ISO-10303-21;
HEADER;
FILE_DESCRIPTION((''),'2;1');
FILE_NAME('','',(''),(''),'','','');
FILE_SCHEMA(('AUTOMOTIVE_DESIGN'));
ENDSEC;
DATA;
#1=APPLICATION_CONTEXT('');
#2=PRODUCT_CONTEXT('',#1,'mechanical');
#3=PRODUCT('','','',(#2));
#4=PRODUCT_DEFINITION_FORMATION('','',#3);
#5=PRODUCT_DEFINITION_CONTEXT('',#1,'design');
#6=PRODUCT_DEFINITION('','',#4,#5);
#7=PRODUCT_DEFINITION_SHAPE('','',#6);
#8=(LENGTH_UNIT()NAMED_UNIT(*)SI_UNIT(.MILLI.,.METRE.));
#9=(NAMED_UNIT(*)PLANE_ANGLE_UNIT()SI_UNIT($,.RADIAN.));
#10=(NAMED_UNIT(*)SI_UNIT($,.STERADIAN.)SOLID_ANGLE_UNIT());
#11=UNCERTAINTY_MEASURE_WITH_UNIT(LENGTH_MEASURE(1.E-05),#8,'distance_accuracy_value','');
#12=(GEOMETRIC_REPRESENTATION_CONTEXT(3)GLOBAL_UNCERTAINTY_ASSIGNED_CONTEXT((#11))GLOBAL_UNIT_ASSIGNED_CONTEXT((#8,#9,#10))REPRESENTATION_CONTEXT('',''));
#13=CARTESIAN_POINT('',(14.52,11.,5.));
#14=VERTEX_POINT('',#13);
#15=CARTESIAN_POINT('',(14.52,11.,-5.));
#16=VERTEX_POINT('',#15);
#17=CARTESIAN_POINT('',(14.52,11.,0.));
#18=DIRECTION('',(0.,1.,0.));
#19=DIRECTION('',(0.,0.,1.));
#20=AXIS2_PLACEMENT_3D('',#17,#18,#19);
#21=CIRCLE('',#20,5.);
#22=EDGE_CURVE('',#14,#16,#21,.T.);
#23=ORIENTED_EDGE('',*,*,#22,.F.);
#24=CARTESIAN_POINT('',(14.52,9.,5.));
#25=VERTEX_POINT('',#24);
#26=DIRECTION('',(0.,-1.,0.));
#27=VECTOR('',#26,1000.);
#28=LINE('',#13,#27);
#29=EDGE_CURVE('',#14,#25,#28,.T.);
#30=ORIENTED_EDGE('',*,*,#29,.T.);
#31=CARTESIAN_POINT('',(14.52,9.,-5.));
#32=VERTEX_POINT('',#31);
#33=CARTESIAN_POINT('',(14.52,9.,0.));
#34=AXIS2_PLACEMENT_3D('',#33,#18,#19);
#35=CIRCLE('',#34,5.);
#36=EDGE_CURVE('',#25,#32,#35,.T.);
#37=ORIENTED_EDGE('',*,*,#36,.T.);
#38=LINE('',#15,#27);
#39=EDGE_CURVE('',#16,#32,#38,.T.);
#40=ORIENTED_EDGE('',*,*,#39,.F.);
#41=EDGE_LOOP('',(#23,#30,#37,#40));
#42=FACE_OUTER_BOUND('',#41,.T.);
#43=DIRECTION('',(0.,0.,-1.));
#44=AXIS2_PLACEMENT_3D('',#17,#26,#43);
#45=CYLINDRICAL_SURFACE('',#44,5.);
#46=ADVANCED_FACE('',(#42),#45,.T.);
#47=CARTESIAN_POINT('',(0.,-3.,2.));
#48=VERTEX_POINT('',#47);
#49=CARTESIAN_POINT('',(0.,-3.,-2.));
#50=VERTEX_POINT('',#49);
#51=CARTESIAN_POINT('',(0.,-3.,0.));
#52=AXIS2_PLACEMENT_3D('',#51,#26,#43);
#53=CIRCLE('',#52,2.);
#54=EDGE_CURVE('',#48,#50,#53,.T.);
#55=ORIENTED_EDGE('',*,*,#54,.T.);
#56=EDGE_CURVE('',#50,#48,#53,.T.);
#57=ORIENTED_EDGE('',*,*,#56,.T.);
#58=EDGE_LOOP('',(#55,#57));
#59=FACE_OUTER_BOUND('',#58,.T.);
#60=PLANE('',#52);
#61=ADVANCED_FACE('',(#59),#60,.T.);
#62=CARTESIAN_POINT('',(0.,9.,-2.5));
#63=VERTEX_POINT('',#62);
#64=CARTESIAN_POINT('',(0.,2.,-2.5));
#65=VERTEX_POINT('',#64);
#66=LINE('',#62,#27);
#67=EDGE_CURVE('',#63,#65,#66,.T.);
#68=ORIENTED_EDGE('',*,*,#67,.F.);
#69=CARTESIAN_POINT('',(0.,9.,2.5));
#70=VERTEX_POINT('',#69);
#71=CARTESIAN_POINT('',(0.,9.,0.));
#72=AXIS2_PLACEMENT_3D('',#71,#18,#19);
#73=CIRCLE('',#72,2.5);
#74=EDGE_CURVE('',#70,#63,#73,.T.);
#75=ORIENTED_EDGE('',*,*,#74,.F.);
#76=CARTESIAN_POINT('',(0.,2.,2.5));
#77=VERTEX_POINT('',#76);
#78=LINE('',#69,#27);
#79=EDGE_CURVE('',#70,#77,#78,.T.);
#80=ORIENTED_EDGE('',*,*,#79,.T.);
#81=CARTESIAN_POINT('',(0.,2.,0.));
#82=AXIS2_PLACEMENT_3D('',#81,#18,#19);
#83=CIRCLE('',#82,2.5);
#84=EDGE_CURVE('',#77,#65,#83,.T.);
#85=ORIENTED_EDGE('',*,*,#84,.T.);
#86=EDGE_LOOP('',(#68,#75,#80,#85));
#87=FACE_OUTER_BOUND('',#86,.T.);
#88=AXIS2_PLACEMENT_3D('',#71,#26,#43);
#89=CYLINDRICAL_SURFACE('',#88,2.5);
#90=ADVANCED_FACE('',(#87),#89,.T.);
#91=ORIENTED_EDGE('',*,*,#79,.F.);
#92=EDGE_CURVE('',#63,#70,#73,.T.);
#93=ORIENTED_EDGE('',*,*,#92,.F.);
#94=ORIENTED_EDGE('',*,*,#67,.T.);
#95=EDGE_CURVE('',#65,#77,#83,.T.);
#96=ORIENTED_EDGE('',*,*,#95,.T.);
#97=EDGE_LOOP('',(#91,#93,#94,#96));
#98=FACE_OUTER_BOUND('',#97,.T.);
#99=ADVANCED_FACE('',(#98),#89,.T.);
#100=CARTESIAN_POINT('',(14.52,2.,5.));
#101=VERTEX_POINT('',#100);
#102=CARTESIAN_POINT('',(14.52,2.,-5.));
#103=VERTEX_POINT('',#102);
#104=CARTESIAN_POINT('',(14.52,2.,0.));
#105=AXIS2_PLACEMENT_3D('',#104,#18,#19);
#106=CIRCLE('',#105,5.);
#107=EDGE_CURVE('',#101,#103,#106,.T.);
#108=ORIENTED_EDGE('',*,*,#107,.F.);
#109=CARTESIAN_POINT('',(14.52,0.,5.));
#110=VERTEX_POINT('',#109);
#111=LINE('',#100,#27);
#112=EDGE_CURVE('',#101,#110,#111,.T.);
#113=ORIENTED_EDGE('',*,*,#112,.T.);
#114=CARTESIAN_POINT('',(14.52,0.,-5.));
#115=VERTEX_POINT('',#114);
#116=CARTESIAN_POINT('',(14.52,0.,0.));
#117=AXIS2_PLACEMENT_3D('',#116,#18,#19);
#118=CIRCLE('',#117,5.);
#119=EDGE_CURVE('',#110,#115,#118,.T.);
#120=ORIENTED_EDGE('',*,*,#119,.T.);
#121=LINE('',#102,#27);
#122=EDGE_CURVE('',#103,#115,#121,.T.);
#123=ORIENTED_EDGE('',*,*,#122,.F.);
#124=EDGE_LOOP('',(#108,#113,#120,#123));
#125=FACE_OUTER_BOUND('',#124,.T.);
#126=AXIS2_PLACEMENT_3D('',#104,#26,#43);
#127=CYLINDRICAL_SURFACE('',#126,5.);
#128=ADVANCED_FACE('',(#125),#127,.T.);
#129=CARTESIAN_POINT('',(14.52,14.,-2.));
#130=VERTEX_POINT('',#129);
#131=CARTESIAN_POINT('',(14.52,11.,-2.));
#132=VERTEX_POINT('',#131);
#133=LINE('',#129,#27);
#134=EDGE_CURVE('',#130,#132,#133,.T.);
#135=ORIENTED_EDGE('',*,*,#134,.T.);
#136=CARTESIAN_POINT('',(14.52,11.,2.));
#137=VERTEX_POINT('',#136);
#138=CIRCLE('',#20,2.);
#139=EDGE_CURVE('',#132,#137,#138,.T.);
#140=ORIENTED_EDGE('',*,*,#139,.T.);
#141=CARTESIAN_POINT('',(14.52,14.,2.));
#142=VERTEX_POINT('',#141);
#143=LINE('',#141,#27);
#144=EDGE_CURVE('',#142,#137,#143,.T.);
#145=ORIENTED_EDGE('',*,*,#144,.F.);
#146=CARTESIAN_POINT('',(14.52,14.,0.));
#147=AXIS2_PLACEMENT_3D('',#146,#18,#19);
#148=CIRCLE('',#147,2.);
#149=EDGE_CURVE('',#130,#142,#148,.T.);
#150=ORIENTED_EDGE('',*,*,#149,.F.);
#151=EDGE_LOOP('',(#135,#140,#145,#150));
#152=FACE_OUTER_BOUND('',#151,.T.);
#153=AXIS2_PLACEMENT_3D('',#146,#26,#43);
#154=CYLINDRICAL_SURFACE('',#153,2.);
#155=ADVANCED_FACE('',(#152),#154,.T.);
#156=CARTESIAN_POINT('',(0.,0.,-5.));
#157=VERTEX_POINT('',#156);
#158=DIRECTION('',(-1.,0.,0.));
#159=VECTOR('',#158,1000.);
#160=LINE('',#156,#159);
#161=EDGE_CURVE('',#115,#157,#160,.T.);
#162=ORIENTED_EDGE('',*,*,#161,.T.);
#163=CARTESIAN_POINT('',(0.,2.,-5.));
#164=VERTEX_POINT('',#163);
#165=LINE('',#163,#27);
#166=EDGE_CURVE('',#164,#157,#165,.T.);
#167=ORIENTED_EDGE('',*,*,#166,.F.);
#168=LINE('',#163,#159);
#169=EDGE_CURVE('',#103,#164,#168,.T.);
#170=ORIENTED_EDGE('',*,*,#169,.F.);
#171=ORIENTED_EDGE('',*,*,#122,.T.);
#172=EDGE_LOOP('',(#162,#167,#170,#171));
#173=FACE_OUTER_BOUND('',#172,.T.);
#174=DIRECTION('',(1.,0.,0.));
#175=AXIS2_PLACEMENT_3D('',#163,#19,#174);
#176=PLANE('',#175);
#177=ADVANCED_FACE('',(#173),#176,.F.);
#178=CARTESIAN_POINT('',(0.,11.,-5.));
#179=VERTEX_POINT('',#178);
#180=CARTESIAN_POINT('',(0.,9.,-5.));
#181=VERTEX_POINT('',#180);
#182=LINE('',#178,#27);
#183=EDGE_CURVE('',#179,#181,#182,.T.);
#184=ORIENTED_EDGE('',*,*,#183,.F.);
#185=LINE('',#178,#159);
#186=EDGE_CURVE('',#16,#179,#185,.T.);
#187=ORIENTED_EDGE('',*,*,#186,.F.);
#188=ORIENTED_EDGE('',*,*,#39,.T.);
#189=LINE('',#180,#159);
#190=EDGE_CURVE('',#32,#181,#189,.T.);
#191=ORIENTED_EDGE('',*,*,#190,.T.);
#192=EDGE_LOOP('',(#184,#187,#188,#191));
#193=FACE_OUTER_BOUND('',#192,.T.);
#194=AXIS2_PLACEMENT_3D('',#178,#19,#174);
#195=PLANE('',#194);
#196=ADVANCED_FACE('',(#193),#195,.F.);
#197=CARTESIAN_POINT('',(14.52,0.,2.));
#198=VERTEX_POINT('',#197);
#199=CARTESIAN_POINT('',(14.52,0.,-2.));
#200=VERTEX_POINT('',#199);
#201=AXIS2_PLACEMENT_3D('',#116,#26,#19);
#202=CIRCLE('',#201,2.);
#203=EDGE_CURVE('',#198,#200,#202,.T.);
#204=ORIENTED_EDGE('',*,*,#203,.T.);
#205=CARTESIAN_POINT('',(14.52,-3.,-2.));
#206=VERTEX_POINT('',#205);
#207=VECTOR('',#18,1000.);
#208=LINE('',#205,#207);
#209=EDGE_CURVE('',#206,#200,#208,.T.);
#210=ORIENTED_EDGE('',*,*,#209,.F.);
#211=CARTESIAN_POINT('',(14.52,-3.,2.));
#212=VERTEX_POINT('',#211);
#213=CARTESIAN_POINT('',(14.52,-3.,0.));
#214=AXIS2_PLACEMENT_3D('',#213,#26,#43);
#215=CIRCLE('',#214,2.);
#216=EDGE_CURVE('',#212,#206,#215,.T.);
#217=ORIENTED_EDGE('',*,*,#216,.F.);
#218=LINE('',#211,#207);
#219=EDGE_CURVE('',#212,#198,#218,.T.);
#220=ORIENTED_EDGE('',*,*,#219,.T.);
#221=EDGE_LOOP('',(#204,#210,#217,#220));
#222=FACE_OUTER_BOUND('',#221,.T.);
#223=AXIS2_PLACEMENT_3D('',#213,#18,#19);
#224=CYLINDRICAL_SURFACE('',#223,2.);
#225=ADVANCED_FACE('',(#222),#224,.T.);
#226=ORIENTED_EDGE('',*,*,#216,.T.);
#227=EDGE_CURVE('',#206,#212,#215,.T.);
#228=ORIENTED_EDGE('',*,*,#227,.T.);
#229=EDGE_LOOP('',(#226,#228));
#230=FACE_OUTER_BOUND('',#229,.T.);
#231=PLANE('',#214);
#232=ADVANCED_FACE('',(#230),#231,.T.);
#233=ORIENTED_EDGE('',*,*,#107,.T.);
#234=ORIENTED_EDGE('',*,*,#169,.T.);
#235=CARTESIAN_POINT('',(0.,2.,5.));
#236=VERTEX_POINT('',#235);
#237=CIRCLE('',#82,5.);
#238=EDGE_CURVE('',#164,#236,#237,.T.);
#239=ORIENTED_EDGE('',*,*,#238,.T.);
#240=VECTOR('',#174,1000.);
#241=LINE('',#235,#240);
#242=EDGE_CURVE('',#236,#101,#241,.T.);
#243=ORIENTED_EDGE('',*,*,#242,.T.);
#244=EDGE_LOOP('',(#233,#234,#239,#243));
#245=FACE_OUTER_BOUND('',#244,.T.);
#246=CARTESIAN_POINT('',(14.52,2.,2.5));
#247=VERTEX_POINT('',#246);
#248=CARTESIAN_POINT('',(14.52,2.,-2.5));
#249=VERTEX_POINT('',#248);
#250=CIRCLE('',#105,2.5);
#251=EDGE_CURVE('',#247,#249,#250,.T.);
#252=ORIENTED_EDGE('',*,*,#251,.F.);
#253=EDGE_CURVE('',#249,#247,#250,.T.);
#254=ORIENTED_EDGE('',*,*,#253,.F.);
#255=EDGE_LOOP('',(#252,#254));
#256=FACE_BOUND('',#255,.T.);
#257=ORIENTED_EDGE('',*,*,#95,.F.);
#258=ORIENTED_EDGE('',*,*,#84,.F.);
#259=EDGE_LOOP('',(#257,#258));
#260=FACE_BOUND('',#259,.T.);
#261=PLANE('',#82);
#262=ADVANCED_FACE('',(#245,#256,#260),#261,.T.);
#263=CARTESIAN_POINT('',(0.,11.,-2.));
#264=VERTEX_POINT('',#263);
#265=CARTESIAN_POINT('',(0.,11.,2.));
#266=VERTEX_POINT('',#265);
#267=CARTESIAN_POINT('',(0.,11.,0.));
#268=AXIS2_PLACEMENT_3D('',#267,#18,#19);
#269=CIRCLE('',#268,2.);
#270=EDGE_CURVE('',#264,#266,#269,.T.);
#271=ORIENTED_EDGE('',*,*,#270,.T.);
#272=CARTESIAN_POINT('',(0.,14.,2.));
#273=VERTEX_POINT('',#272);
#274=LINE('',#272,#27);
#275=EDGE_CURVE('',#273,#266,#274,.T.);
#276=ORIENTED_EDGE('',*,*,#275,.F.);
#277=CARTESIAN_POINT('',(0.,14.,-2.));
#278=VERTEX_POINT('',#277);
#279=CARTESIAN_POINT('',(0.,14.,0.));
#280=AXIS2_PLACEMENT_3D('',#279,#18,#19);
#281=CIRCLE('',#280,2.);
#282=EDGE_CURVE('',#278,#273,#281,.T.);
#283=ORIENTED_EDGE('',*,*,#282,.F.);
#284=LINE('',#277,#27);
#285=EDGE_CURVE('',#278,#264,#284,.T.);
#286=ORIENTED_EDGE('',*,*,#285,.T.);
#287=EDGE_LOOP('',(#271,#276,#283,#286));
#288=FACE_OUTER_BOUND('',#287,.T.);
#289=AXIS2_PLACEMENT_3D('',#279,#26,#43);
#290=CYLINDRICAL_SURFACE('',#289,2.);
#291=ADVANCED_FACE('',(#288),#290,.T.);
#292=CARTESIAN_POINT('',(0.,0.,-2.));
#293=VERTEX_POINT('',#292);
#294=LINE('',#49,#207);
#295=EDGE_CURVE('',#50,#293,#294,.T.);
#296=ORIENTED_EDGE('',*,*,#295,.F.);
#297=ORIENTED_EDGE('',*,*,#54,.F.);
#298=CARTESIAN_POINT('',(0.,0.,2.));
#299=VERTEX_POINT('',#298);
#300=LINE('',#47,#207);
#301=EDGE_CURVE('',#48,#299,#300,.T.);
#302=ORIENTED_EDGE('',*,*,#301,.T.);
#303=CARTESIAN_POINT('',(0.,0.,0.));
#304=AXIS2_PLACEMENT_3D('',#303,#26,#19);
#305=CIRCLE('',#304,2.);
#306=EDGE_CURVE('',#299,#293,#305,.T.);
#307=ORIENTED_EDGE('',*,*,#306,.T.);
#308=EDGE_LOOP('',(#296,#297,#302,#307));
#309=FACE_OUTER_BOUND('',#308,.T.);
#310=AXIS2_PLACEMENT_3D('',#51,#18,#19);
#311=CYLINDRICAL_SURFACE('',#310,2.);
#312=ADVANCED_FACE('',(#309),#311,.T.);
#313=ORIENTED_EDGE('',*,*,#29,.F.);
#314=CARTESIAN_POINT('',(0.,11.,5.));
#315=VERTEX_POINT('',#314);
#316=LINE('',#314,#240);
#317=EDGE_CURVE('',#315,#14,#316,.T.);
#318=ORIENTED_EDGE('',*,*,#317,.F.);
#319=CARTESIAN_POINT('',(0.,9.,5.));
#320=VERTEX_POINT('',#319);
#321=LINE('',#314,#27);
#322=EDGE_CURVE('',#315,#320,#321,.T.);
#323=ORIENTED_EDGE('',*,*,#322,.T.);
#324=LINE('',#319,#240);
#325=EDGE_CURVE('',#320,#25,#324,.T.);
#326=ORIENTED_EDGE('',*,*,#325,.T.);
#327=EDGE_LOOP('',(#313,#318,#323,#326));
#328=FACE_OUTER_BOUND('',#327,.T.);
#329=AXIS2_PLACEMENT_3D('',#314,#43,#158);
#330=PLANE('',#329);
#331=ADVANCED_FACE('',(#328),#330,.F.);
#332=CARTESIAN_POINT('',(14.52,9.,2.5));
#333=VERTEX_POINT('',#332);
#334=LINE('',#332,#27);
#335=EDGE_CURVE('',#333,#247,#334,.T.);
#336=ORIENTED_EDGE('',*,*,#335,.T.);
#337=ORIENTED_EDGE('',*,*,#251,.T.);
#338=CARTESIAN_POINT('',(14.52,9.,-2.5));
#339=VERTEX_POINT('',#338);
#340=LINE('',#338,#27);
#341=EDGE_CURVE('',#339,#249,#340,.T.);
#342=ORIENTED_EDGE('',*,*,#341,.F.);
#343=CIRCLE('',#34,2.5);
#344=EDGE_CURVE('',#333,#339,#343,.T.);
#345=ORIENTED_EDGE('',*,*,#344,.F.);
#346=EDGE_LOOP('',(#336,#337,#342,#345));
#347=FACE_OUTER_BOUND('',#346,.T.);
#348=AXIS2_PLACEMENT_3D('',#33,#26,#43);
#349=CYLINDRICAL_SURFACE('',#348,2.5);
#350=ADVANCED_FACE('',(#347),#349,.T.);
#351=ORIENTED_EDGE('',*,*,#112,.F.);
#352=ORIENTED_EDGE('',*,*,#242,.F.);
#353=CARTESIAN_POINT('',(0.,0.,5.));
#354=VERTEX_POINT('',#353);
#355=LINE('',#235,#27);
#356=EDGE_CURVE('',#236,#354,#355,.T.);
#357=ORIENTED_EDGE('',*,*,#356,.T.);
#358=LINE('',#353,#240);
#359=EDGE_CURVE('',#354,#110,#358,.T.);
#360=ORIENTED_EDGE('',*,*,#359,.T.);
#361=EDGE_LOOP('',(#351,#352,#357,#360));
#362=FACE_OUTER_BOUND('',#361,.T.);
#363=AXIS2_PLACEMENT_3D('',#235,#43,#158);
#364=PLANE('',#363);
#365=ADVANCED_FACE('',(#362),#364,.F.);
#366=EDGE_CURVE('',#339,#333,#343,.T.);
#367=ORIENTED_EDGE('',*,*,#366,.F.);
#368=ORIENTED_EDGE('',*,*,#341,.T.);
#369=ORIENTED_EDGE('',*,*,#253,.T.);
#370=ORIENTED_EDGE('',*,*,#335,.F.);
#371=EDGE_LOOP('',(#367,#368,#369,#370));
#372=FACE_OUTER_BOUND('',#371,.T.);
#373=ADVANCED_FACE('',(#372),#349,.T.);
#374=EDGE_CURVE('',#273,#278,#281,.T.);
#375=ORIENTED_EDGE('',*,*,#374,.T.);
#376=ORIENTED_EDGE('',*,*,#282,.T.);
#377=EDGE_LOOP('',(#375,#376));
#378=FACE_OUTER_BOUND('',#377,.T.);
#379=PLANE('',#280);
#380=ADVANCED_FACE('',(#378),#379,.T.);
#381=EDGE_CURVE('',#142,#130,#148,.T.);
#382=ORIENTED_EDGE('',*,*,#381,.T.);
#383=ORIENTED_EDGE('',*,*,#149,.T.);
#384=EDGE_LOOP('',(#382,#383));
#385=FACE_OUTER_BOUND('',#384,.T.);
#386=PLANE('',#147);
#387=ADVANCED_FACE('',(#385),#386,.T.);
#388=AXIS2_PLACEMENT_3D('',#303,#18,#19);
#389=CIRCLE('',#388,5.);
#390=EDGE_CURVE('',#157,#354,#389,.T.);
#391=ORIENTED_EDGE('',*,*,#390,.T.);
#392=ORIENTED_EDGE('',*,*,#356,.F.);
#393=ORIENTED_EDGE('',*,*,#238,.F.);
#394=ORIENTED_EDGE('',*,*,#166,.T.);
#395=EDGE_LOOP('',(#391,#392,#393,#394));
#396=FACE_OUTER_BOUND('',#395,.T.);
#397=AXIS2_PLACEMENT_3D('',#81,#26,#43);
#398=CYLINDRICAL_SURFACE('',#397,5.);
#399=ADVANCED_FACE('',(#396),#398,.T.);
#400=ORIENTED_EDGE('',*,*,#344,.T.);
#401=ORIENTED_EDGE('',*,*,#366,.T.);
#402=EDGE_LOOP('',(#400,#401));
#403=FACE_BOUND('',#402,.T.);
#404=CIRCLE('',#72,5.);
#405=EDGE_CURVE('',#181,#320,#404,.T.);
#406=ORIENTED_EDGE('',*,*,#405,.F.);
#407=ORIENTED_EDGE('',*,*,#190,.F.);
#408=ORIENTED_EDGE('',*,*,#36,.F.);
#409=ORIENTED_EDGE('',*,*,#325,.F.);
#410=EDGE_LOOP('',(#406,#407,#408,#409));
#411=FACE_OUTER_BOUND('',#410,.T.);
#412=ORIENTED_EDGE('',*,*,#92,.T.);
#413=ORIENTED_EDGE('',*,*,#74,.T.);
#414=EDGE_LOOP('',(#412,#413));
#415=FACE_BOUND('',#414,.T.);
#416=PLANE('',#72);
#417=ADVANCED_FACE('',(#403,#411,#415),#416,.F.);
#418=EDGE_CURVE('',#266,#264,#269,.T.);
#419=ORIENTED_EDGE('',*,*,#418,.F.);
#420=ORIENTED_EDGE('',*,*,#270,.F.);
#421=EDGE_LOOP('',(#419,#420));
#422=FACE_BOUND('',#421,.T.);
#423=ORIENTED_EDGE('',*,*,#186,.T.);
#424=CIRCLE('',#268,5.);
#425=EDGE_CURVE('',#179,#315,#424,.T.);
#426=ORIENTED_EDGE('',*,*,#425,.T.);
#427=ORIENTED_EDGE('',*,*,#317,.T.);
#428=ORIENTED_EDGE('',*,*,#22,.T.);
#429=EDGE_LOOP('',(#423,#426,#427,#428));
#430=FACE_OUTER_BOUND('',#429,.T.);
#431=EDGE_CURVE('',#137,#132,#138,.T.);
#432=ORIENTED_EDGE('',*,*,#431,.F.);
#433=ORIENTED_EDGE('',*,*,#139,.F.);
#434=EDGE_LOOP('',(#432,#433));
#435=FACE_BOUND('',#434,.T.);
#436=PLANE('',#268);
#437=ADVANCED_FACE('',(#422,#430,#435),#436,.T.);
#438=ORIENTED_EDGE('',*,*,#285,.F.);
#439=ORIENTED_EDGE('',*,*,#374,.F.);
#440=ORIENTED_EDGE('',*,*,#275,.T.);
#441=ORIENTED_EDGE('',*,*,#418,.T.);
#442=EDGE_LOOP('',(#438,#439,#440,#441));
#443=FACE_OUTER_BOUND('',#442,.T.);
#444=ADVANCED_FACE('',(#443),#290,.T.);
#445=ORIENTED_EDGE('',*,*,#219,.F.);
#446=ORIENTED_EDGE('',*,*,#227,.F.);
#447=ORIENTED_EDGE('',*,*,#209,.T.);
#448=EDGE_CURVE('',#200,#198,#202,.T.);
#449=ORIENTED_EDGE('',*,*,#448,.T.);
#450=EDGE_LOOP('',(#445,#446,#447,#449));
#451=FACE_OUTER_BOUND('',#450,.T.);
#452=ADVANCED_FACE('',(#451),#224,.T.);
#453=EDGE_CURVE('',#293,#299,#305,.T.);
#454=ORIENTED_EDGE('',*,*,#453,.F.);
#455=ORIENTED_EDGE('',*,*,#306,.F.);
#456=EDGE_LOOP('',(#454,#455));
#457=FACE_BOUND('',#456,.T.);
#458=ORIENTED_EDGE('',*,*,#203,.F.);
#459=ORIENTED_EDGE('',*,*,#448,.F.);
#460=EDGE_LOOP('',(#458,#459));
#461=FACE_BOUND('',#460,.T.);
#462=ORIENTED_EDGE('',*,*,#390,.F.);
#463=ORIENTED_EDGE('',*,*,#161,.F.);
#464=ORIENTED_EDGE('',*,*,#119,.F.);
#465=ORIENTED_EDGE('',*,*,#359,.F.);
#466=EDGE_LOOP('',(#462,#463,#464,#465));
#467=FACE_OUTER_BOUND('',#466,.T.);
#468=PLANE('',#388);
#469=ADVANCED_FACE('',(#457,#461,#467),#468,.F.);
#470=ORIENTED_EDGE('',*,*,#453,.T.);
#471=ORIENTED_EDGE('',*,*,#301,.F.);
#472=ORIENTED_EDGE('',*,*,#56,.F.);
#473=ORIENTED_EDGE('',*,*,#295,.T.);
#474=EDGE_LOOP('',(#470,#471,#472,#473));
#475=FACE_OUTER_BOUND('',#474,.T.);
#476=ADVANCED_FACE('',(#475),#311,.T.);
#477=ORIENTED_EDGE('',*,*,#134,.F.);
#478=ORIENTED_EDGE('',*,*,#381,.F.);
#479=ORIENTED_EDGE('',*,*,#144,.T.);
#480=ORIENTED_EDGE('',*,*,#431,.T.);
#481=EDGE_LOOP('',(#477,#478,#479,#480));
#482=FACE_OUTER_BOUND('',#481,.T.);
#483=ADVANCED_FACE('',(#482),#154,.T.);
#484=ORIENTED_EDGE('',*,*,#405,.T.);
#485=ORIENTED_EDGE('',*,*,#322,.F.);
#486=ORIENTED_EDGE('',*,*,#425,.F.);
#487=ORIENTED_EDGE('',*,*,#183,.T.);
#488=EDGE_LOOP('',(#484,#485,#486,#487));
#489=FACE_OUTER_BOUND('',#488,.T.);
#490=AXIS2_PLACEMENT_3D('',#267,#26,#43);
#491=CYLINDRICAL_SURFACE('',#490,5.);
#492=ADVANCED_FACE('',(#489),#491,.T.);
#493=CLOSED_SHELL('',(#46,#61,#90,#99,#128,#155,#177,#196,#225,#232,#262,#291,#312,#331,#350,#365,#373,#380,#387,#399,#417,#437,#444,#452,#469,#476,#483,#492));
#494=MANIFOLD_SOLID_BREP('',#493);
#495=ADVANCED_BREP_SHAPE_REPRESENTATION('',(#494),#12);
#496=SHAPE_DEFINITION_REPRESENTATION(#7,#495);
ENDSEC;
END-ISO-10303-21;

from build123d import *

# Parameters (mm, degrees)
BOSS_EXTRUDE1_DEPTH = 2
SKETCH2_R           = 2.5
BOSS_EXTRUDE2_DEPTH = 7
BOSS_EXTRUDE3_DEPTH = 2
SKETCH4_R           = 2
BOSS_EXTRUDE4_DEPTH = 3
BOSS_EXTRUDE5_START = 3
SKETCH5_R           = 2
BOSS_EXTRUDE5_DEPTH = 3


with BuildPart() as part:
    # Sketch1 → Boss-Extrude1 (new body)
    with BuildSketch(Plane(origin=(0, 0, 0), x_dir=(1, 0, 0), z_dir=(0, 1, 0))):
        with BuildLine():
            Line((0, 5), (14.52, 5))
            ThreePointArc((14.52, 5), (19.52, 0), (14.52, -5))
            Line((14.52, -5), (0, -5))
            ThreePointArc((0, -5), (-5, 0), (0, 5))
        make_face()
    extrude(amount=BOSS_EXTRUDE1_DEPTH)

    # Sketch2 → Boss-Extrude2 (add)
    with BuildSketch(Plane(origin=(0, 2, 0), x_dir=(1, 0, 0), z_dir=(0, 1, 0))):
        with Locations(Location((0, 0, 0), (0, 0, 270))):
            Circle(SKETCH2_R)
        with Locations(Location((14.52, 0, 0), (0, 0, 270))):
            Circle(SKETCH2_R)
    extrude(amount=BOSS_EXTRUDE2_DEPTH)

    # Sketch3 → Boss-Extrude3 (add)
    with BuildSketch(Plane(origin=(0, 9, 0), x_dir=(1, 0, 0), z_dir=(0, 1, 0))):
        with BuildLine():
            Line((0, 5), (14.52, 5))
            ThreePointArc((14.52, 5), (19.52, 0), (14.52, -5))
            Line((14.52, -5), (0, -5))
            ThreePointArc((0, -5), (-5, 0), (0, 5))
        make_face()
    extrude(amount=BOSS_EXTRUDE3_DEPTH)

    # Sketch4 → Boss-Extrude4 (add)
    with BuildSketch(Plane(origin=(0, 11, 0), x_dir=(1, 0, 0), z_dir=(0, 1, 0))):
        with Locations(Location((0, 0, 0), (0, 0, 270))):
            Circle(SKETCH4_R)
        with Locations(Location((14.52, 0, 0), (0, 0, 270))):
            Circle(SKETCH4_R)
    extrude(amount=BOSS_EXTRUDE4_DEPTH)

    # Sketch5 → Boss-Extrude5 (add)
    with BuildSketch(Plane.XZ.offset(BOSS_EXTRUDE5_START)):
        with Locations(Location((0, 0, 0), (0, 0, 90))):
            Circle(SKETCH5_R)
        with Locations(Location((14.52, 0, 0), (0, 0, 90))):
            Circle(SKETCH5_R)
    extrude(amount=-BOSS_EXTRUDE5_DEPTH)


solid = part.part
